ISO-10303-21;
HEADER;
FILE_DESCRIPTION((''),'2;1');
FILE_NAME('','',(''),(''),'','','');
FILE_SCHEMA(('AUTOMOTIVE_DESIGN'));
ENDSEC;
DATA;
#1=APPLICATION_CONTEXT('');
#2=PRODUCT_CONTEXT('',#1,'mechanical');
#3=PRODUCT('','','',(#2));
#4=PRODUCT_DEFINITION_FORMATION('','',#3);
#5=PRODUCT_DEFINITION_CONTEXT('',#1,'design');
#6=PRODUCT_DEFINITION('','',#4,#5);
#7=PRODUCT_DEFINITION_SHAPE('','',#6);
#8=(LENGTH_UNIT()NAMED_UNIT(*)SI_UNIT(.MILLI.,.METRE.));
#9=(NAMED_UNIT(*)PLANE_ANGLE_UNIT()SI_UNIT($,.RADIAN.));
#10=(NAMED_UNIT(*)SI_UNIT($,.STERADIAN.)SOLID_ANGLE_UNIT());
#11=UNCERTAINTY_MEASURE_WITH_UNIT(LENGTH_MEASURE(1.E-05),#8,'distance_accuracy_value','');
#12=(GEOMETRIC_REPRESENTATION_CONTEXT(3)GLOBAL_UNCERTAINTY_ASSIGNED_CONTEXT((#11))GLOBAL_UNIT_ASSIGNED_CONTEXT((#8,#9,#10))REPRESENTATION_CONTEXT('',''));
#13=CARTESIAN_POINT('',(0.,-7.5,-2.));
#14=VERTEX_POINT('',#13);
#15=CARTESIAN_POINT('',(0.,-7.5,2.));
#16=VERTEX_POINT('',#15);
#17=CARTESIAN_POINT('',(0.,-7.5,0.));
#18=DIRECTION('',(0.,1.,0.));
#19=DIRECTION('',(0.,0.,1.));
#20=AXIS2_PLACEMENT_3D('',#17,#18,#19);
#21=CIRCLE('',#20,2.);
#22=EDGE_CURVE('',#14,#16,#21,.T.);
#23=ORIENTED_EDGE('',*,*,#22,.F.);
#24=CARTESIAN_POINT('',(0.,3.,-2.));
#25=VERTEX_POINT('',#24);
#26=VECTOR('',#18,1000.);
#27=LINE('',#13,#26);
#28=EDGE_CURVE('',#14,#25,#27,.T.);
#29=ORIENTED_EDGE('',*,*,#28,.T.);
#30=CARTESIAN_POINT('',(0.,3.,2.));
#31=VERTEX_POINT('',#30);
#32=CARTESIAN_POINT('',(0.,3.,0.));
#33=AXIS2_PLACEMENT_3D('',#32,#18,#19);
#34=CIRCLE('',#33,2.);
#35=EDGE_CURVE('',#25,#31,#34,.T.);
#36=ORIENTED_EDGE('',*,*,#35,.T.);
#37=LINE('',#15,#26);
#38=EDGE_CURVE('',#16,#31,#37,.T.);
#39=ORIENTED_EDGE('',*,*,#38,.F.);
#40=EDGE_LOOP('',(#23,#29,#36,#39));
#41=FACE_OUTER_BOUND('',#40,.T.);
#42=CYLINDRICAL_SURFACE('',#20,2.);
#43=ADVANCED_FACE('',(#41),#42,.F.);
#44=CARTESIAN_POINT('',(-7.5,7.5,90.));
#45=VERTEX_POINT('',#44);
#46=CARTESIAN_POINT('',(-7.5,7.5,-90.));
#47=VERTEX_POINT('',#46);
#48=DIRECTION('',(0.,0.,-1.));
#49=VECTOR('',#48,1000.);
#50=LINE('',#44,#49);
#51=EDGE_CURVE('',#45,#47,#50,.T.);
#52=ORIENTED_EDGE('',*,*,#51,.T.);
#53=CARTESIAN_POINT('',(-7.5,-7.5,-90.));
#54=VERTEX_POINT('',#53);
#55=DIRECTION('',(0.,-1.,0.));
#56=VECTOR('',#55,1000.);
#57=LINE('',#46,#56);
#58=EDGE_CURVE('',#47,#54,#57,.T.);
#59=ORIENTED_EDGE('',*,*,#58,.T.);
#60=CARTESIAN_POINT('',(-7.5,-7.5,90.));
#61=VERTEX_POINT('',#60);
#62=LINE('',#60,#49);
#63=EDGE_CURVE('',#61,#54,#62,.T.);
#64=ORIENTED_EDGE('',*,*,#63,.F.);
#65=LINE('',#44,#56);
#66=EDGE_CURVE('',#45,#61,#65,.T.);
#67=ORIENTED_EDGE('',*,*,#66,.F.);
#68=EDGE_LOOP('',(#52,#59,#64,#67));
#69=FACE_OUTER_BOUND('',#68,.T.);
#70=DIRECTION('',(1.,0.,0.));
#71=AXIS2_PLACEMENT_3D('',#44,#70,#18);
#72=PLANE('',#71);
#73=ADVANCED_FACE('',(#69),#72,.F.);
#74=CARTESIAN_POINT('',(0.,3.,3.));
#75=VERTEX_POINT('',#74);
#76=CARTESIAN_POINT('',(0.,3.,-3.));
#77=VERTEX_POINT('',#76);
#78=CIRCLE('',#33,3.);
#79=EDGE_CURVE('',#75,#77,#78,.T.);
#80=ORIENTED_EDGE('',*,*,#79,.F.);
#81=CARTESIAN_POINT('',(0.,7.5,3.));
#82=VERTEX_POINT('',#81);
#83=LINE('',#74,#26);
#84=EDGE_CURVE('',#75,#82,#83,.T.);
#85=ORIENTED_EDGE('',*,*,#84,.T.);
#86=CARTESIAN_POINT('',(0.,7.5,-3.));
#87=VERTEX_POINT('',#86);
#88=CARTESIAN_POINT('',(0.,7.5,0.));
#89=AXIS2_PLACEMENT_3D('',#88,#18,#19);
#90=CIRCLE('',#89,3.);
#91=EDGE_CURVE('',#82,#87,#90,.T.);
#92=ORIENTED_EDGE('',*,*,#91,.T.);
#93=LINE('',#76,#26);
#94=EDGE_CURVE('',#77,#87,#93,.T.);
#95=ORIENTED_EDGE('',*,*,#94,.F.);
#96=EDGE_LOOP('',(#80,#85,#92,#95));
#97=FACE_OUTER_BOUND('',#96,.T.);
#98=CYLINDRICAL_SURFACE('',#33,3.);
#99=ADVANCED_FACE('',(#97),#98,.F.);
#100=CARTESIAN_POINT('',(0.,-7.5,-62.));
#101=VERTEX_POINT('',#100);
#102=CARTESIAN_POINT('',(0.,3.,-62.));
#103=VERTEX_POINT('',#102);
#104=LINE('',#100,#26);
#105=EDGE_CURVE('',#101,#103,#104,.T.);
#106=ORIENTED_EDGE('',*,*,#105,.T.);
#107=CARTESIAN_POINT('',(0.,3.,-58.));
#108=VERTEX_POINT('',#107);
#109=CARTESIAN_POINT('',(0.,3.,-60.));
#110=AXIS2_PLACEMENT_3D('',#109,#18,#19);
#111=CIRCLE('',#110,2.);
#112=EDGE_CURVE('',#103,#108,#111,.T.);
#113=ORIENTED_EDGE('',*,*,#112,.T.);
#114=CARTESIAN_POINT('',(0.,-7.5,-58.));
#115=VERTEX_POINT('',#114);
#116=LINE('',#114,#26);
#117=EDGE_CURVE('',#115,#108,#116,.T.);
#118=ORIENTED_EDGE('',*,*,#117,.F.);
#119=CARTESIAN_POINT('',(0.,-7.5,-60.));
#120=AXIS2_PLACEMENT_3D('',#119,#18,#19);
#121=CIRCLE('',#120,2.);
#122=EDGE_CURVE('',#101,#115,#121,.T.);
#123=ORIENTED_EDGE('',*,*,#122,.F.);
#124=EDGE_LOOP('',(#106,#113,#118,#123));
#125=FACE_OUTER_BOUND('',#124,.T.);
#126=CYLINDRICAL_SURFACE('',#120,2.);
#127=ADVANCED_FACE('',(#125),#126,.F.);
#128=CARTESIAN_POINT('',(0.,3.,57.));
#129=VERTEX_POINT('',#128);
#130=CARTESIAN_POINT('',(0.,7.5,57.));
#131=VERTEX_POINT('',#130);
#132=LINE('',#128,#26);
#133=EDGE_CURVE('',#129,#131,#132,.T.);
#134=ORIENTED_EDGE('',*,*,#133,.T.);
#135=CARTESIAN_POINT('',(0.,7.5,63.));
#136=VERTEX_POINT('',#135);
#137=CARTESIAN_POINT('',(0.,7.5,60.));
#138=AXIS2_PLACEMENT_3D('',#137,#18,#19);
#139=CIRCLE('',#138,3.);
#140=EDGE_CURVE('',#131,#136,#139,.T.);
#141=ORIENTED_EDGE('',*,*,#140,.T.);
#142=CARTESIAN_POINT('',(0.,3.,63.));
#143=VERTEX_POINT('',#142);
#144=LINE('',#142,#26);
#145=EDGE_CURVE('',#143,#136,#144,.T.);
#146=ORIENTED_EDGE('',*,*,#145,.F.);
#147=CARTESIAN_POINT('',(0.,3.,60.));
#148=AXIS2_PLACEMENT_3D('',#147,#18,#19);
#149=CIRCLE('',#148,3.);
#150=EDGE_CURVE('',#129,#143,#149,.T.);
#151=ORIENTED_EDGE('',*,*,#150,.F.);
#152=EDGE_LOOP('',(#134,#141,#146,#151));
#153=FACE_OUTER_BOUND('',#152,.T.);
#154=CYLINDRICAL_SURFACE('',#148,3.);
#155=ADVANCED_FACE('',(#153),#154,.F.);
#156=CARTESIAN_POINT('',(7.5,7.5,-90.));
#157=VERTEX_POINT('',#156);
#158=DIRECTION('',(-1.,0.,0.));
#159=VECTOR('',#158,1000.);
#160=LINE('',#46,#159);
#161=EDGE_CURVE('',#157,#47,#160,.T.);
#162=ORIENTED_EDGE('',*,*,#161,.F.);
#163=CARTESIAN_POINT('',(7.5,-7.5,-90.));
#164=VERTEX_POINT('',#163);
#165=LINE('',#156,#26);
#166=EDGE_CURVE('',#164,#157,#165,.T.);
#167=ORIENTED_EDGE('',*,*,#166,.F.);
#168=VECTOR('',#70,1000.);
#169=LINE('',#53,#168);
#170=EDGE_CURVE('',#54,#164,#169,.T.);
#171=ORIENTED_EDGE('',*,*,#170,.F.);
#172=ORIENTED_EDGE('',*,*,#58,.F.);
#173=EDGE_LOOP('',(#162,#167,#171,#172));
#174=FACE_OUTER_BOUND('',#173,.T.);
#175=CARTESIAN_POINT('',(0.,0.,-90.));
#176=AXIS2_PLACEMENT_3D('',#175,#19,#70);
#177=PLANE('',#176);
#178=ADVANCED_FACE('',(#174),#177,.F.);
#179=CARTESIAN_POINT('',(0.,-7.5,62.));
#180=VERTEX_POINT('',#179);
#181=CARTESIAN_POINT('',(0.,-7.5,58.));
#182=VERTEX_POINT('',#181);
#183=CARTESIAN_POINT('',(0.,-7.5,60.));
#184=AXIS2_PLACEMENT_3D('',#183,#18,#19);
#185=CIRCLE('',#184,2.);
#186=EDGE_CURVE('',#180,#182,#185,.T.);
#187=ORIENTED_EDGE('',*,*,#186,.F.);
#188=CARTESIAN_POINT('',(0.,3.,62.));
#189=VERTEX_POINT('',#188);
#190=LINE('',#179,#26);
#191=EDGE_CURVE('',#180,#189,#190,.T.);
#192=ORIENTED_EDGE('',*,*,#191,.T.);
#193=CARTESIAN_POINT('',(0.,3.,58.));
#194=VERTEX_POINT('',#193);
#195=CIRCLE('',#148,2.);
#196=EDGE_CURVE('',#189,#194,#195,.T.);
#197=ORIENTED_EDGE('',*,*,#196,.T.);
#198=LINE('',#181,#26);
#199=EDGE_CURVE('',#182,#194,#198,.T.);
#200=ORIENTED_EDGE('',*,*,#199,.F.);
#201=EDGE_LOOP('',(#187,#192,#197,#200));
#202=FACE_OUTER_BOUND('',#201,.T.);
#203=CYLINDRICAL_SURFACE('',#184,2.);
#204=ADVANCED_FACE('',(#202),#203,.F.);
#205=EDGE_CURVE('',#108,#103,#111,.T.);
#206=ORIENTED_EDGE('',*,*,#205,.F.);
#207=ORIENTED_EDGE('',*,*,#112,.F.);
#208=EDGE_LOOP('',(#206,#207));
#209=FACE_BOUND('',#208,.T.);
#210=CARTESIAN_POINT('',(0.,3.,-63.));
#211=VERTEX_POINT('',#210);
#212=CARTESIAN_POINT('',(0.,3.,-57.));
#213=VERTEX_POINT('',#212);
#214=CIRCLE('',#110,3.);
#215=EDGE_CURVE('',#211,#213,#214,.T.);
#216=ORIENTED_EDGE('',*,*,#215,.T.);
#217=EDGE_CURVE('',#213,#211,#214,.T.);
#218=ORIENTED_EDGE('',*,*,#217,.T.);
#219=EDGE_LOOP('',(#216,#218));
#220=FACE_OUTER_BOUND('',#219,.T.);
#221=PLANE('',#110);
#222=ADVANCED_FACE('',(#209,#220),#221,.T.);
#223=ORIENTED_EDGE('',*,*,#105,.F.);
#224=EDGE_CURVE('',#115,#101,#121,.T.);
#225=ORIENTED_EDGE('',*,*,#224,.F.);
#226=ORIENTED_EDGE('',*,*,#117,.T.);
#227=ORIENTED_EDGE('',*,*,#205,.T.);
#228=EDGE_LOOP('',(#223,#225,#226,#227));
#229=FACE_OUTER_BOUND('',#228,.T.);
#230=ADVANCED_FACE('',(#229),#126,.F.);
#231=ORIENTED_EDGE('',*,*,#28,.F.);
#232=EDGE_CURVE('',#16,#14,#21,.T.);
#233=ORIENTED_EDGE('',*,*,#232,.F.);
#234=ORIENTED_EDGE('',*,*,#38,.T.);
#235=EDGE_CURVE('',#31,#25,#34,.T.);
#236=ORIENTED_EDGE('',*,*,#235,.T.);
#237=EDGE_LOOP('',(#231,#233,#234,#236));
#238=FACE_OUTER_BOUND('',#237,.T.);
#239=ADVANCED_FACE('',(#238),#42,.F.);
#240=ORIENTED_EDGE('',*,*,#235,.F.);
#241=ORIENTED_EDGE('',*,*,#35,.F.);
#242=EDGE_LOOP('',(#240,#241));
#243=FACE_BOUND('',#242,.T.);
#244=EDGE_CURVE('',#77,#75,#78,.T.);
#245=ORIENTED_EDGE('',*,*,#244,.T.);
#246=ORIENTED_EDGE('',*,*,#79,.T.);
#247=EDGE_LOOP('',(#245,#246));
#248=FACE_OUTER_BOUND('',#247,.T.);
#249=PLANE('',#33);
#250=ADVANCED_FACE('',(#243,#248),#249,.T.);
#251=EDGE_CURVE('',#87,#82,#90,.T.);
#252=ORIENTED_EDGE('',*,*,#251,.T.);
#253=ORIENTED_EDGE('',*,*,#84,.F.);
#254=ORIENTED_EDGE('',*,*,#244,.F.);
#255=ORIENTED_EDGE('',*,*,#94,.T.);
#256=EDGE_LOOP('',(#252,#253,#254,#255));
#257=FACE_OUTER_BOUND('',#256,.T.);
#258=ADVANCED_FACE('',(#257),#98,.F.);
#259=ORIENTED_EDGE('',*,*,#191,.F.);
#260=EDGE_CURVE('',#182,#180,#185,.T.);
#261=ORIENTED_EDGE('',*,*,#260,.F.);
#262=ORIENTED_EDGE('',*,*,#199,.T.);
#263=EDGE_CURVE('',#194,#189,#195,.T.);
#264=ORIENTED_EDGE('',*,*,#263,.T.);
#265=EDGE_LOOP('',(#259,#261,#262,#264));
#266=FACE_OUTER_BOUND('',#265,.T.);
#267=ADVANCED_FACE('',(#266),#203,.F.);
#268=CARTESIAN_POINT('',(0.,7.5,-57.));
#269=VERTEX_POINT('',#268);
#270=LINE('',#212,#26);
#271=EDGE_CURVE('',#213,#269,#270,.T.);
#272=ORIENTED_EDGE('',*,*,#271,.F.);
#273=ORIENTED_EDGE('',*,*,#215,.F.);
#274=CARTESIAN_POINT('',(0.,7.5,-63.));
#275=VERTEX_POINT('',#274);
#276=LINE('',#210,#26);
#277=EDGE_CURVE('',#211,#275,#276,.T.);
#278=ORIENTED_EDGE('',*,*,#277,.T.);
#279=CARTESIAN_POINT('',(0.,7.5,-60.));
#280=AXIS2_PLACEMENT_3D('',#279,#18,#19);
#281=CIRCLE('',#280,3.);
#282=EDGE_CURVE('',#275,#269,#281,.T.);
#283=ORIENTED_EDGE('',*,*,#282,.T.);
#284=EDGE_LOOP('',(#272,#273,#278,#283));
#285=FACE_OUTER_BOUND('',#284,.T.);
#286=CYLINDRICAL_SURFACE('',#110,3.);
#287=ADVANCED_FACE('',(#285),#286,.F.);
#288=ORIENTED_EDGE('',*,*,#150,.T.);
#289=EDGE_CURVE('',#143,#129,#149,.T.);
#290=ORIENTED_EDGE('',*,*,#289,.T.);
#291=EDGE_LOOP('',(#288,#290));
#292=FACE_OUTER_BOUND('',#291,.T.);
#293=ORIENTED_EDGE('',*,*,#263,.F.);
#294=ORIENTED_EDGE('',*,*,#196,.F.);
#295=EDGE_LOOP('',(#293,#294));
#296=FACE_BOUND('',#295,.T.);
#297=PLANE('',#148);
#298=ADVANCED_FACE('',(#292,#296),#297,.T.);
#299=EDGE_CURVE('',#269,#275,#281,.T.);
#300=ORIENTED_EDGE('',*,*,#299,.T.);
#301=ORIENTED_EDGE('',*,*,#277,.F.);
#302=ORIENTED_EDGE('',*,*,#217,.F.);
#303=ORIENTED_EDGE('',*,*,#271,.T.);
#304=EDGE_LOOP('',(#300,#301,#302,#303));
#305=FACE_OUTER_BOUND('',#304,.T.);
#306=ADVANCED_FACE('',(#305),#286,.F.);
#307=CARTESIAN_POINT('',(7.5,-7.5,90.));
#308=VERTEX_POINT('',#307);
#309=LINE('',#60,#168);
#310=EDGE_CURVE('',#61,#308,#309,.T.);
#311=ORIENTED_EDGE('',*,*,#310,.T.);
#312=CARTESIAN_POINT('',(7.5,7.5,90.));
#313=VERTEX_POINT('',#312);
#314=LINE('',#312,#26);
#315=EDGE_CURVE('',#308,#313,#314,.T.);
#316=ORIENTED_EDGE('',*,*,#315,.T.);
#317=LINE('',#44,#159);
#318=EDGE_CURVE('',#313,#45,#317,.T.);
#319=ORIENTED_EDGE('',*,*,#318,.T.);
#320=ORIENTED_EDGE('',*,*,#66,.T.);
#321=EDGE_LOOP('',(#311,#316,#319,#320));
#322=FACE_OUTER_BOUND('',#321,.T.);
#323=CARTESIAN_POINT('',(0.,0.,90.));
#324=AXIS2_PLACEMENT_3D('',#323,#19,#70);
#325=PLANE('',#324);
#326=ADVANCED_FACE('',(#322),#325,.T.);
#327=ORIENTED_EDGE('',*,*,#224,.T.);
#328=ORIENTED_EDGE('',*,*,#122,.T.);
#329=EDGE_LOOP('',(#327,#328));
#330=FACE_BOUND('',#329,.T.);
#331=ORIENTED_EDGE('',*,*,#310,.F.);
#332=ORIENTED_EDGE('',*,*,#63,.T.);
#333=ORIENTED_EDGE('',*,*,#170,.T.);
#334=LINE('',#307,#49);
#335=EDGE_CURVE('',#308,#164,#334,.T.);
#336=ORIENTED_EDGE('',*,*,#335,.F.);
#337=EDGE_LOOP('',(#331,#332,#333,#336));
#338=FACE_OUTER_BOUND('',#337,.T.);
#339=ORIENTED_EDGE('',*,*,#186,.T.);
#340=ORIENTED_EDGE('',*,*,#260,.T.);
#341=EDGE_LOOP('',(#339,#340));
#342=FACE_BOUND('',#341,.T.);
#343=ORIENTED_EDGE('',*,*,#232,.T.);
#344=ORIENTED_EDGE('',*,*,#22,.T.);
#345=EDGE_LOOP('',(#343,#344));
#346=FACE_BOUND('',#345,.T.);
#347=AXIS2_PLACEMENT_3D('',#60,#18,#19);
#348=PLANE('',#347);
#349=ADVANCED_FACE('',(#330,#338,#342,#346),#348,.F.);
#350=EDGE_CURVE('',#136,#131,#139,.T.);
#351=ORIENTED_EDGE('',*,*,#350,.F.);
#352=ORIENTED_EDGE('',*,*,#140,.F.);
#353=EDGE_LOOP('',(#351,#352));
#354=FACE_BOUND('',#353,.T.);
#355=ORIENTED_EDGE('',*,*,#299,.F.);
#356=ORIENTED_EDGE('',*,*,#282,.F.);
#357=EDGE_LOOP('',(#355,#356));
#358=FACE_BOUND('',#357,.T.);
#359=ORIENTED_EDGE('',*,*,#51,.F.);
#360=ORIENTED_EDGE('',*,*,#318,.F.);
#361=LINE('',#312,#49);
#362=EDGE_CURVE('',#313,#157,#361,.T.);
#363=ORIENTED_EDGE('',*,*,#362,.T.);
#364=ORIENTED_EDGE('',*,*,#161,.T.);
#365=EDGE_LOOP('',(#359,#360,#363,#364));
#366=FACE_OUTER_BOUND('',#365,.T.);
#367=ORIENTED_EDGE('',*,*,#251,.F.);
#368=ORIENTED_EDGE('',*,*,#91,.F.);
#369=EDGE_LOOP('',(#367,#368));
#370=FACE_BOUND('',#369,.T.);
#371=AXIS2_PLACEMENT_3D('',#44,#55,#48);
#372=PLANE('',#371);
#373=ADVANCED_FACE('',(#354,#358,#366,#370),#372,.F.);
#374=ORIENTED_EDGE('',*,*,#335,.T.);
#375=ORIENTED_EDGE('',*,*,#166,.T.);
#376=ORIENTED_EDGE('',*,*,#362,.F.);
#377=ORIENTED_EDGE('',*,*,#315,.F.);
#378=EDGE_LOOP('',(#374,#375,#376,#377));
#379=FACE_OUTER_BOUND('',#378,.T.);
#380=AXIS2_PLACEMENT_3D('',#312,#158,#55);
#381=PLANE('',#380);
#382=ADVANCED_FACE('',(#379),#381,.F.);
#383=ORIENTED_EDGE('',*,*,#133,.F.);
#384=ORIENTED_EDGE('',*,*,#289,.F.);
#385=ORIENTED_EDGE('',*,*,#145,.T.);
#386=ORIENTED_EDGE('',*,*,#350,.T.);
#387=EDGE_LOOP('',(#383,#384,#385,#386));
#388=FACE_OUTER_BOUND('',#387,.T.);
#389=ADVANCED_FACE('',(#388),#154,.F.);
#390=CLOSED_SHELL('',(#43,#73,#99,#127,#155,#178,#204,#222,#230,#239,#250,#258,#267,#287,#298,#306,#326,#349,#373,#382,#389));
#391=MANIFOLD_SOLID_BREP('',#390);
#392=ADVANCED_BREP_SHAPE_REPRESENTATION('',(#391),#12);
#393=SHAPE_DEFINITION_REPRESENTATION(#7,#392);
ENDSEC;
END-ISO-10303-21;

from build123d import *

# Parameters (mm, degrees)
SKETCH_1_W             = 15
SKETCH_1_H             = 15
EXTRUDE_1_DEPTH        = 90
SKETCH_2_R             = 3
CUT_EXTRUDE_1_DEPTH    = 4.5
SKETCH_3_R             = 2
CUT_EXTRUDE_2_DEPTH    = 92.549167118
PATTERN_LINEAR_1_COUNT = 4
PATTERN_LINEAR_1_PITCH = 60


with BuildPart() as part:
    # 草图1 → 凸台-拉伸1 (new, symmetric)
    with BuildSketch(Plane.XY):
        Rectangle(SKETCH_1_W, SKETCH_1_H)
    extrude(amount=EXTRUDE_1_DEPTH, both=True)

    # 草图2 → 切除-拉伸1 (cut)
    with BuildSketch(Plane(origin=(0, 7.5, 0), x_dir=(1, 0, 0), z_dir=(0, 1, 0))):
        with Locations(Location((0, -60, 0), (0, 0, 270))):
            Circle(SKETCH_2_R)
    cut_extrude_1 = extrude(amount=-CUT_EXTRUDE_1_DEPTH, mode=Mode.SUBTRACT)

    # 草图3 → 切除-拉伸2 (cut, through all)
    with BuildSketch(Plane(origin=(0, 7.5, 0), x_dir=(1, 0, 0), z_dir=(0, 1, 0))):
        with Locations(Location((0, -60, 0), (0, 0, 270))):
            Circle(SKETCH_3_R)
    cut_extrude_2 = extrude(amount=-CUT_EXTRUDE_2_DEPTH, mode=Mode.SUBTRACT)

    # 阵列(线性)1: 切除-拉伸1, 切除-拉伸2 ×4
    with Locations(*[(0, 0, -i * PATTERN_LINEAR_1_PITCH) for i in range(1, PATTERN_LINEAR_1_COUNT)]):
        add(cut_extrude_1, mode=Mode.SUBTRACT)
        add(cut_extrude_2, mode=Mode.SUBTRACT)


solid = part.part
